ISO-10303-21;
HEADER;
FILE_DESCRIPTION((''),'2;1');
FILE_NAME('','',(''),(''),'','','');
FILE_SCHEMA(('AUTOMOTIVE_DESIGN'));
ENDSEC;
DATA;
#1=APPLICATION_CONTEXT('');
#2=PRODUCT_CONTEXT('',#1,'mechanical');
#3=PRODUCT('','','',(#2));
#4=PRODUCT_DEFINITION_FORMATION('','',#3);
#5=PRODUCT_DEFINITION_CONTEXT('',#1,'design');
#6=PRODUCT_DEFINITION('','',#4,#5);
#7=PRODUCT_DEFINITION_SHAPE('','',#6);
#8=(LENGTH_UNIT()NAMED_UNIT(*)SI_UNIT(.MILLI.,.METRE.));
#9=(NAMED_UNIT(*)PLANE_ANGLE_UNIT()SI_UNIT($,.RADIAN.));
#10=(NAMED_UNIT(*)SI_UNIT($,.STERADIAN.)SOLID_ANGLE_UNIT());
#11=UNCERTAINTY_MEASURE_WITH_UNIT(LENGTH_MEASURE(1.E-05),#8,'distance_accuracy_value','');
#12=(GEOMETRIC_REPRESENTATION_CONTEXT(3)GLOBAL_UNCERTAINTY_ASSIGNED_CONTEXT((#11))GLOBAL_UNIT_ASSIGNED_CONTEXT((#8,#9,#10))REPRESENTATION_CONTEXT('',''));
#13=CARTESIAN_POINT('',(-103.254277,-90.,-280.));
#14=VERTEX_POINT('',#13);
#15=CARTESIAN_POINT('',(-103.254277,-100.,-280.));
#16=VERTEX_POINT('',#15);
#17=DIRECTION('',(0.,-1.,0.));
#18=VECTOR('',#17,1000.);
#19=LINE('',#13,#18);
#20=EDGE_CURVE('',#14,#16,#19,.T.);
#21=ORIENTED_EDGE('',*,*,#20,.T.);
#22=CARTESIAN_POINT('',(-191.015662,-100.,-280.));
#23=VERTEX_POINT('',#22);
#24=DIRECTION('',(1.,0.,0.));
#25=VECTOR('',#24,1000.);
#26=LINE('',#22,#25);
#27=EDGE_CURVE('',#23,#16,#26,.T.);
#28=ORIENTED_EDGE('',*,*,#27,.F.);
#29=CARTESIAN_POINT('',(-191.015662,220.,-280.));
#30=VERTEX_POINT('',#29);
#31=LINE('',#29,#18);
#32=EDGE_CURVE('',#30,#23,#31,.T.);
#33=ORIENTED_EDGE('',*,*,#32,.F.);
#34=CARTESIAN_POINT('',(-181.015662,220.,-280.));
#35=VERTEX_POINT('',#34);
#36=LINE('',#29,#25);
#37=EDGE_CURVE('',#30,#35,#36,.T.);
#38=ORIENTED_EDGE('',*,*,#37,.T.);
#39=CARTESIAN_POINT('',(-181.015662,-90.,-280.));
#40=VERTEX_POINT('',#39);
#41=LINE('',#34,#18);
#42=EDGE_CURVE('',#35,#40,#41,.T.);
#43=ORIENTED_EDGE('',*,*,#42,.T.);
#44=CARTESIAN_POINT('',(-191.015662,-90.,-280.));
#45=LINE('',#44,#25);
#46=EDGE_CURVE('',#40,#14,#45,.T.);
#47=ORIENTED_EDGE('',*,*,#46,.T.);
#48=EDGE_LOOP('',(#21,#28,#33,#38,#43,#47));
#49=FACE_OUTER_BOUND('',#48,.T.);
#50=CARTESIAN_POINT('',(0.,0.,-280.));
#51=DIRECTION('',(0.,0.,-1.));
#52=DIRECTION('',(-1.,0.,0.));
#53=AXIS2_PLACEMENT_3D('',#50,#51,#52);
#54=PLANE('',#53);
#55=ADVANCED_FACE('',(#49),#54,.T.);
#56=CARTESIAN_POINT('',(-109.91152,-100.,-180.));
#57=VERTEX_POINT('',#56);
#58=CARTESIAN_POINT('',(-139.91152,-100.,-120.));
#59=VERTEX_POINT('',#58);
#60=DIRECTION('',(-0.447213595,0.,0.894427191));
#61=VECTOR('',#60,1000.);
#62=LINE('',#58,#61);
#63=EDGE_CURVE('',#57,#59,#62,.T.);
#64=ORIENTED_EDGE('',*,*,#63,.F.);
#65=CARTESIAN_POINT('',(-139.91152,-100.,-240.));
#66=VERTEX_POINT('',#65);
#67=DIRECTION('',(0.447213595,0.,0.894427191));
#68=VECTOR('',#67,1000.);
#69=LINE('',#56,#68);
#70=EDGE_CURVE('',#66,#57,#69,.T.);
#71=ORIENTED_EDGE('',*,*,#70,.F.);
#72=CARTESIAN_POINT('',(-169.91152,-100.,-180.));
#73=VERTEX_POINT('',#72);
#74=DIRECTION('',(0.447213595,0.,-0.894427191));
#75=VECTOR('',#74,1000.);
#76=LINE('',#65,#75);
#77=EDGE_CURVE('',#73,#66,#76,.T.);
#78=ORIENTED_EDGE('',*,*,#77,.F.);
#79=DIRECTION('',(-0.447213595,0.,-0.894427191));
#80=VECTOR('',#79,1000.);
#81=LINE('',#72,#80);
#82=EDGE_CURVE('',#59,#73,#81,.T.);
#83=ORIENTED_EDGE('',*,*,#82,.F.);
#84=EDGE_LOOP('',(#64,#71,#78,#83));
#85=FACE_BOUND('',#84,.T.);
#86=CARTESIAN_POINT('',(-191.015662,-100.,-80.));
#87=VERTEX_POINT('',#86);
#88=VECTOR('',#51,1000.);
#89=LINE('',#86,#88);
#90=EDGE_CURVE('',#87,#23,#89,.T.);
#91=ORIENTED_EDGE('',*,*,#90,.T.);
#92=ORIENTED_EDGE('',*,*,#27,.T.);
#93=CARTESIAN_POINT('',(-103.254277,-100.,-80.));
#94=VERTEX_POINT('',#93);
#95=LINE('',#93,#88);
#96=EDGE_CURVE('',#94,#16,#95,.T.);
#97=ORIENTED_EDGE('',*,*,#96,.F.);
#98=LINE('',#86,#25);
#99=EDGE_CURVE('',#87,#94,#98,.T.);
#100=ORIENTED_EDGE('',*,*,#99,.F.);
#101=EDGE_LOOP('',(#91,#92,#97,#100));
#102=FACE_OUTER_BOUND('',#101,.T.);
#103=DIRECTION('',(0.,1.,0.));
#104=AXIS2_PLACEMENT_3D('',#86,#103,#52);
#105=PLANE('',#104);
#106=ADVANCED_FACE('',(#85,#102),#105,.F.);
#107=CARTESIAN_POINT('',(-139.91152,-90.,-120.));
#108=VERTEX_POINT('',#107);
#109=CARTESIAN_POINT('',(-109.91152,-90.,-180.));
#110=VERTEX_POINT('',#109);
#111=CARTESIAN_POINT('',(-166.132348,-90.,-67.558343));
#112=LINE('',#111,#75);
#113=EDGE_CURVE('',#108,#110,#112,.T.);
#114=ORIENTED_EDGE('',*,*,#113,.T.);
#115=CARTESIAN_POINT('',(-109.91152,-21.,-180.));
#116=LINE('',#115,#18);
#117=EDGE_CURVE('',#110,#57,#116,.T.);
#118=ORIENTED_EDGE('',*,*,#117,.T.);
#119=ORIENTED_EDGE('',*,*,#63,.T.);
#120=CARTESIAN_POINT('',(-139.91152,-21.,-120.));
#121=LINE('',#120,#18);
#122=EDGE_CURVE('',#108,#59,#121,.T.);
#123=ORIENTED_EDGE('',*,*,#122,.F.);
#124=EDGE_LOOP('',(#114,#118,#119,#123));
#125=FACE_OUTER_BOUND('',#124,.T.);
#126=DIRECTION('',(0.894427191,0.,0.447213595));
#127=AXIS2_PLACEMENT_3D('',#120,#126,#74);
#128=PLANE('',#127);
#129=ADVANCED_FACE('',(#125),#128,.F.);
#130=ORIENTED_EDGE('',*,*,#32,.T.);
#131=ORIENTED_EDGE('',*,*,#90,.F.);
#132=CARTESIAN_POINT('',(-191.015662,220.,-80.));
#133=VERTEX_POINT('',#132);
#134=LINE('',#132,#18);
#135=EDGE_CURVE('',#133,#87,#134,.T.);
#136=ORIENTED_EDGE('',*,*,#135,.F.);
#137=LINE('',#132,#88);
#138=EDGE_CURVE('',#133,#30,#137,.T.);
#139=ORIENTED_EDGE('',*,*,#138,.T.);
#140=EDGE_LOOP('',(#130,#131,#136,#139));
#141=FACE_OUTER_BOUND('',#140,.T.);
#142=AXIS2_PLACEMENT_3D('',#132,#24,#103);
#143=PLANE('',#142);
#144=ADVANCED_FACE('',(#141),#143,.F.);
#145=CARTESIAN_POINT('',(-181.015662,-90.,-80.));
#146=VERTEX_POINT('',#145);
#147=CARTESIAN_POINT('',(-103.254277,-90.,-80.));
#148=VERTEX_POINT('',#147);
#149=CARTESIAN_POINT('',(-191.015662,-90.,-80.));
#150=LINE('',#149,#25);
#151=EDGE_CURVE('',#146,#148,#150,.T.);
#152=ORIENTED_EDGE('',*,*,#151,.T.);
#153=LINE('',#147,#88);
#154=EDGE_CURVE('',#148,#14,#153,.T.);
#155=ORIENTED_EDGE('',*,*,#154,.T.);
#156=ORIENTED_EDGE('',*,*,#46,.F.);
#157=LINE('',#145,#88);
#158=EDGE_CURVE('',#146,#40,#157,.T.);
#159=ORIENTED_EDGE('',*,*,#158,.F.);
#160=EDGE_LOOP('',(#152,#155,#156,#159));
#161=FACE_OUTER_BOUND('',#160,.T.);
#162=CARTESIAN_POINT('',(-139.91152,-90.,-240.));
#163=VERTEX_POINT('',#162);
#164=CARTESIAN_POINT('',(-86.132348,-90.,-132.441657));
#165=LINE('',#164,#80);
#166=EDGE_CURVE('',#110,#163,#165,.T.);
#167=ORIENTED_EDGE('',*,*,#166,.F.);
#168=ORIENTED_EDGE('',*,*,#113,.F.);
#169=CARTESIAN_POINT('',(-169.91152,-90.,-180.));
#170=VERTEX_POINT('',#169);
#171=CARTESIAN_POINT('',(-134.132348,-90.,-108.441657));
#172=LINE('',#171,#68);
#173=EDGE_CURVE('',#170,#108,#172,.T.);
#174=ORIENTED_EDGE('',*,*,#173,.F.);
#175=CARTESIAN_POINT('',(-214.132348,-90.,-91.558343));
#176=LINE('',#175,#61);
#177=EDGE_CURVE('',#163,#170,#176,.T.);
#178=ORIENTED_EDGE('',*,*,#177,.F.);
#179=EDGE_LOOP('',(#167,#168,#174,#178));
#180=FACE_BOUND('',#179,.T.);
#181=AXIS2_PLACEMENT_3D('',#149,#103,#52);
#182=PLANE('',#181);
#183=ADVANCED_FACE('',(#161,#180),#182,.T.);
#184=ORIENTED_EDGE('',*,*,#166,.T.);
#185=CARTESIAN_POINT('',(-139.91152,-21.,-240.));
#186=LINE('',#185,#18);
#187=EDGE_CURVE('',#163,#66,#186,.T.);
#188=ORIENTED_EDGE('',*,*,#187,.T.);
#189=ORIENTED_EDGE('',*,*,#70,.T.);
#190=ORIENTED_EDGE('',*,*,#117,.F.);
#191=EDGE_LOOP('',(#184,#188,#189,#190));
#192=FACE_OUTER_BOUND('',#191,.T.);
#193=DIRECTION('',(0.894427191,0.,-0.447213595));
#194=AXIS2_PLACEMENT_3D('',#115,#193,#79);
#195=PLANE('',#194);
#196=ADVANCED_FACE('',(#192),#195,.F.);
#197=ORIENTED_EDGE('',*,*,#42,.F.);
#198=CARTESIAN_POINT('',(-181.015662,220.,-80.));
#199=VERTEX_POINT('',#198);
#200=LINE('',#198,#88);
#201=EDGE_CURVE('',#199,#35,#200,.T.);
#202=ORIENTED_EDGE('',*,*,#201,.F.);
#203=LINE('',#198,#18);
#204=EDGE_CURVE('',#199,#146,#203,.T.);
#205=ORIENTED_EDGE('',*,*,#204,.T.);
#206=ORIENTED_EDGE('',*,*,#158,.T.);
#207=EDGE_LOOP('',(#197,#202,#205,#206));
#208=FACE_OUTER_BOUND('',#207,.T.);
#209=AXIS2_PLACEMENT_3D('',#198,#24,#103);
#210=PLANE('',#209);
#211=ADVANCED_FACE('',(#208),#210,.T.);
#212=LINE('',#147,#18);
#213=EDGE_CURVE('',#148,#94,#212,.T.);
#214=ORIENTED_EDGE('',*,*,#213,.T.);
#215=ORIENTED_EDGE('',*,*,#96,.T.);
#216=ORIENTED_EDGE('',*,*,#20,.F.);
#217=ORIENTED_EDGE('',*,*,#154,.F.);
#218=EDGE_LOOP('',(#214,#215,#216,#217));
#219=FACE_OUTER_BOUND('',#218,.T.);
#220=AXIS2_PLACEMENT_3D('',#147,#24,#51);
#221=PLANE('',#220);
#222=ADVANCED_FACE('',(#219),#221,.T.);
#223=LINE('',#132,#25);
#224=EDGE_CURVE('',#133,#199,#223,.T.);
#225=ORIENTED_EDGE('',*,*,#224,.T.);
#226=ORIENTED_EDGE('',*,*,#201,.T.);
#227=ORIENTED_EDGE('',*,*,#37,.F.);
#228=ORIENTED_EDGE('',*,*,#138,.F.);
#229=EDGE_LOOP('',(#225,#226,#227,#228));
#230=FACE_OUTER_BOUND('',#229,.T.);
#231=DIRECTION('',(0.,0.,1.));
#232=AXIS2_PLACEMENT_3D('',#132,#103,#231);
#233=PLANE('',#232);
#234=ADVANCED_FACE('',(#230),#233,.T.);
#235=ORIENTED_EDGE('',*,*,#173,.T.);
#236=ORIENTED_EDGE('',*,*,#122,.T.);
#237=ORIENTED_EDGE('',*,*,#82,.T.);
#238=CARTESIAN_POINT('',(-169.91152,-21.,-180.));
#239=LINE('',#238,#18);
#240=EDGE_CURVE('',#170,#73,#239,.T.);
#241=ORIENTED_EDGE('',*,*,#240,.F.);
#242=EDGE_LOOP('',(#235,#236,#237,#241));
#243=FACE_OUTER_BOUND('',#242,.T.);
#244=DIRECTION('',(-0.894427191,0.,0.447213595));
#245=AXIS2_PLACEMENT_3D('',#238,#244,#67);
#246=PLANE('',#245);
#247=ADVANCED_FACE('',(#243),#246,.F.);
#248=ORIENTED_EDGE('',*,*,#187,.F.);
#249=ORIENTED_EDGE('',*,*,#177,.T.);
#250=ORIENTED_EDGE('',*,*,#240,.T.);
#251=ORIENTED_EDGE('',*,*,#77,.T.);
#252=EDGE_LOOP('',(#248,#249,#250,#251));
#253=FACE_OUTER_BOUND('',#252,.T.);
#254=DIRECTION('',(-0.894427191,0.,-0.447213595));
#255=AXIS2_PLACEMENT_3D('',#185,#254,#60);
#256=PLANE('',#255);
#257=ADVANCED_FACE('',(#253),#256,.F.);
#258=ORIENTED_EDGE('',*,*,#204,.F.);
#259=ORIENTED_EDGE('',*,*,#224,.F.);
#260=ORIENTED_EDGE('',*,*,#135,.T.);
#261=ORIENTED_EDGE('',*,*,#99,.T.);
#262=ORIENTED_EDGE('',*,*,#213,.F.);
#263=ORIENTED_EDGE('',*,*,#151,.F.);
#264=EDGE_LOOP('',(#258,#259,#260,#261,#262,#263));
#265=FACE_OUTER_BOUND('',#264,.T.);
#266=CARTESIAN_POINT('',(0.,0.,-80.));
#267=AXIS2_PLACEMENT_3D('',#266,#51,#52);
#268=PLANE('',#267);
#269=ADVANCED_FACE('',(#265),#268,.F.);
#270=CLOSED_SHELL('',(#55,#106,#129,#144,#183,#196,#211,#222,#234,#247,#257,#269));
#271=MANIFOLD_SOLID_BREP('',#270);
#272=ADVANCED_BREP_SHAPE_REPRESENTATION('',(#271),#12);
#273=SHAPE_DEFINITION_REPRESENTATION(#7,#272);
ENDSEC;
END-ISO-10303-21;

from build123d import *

# Parameters (mm, degrees)
EXTRUDE_THIN1_DEPTH = 100
CUT_EXTRUDE1_DEPTH  = 79


with BuildPart() as part:
    # Sketch2 → Extrude-Thin1 (new, symmetric)
    with BuildSketch(Plane.XY.offset(-180)):
        Polygon((-191.015662361, 220), (-191.015662361, -100), (-103.254276677, -100), (-103.254276677, -90), (-181.015662361, -90), (-181.015662361, 220), align=None)
    extrude(amount=EXTRUDE_THIN1_DEPTH, both=True)

    # Sketch3 → Cut-Extrude1 (cut)
    with BuildSketch(Plane.XZ.offset(100)):
        Polygon((-139.911519959, -240), (-169.911519959, -180), (-139.911519959, -120), (-109.911519959, -180), align=None)
    extrude(amount=-CUT_EXTRUDE1_DEPTH, mode=Mode.SUBTRACT)


solid = part.part
